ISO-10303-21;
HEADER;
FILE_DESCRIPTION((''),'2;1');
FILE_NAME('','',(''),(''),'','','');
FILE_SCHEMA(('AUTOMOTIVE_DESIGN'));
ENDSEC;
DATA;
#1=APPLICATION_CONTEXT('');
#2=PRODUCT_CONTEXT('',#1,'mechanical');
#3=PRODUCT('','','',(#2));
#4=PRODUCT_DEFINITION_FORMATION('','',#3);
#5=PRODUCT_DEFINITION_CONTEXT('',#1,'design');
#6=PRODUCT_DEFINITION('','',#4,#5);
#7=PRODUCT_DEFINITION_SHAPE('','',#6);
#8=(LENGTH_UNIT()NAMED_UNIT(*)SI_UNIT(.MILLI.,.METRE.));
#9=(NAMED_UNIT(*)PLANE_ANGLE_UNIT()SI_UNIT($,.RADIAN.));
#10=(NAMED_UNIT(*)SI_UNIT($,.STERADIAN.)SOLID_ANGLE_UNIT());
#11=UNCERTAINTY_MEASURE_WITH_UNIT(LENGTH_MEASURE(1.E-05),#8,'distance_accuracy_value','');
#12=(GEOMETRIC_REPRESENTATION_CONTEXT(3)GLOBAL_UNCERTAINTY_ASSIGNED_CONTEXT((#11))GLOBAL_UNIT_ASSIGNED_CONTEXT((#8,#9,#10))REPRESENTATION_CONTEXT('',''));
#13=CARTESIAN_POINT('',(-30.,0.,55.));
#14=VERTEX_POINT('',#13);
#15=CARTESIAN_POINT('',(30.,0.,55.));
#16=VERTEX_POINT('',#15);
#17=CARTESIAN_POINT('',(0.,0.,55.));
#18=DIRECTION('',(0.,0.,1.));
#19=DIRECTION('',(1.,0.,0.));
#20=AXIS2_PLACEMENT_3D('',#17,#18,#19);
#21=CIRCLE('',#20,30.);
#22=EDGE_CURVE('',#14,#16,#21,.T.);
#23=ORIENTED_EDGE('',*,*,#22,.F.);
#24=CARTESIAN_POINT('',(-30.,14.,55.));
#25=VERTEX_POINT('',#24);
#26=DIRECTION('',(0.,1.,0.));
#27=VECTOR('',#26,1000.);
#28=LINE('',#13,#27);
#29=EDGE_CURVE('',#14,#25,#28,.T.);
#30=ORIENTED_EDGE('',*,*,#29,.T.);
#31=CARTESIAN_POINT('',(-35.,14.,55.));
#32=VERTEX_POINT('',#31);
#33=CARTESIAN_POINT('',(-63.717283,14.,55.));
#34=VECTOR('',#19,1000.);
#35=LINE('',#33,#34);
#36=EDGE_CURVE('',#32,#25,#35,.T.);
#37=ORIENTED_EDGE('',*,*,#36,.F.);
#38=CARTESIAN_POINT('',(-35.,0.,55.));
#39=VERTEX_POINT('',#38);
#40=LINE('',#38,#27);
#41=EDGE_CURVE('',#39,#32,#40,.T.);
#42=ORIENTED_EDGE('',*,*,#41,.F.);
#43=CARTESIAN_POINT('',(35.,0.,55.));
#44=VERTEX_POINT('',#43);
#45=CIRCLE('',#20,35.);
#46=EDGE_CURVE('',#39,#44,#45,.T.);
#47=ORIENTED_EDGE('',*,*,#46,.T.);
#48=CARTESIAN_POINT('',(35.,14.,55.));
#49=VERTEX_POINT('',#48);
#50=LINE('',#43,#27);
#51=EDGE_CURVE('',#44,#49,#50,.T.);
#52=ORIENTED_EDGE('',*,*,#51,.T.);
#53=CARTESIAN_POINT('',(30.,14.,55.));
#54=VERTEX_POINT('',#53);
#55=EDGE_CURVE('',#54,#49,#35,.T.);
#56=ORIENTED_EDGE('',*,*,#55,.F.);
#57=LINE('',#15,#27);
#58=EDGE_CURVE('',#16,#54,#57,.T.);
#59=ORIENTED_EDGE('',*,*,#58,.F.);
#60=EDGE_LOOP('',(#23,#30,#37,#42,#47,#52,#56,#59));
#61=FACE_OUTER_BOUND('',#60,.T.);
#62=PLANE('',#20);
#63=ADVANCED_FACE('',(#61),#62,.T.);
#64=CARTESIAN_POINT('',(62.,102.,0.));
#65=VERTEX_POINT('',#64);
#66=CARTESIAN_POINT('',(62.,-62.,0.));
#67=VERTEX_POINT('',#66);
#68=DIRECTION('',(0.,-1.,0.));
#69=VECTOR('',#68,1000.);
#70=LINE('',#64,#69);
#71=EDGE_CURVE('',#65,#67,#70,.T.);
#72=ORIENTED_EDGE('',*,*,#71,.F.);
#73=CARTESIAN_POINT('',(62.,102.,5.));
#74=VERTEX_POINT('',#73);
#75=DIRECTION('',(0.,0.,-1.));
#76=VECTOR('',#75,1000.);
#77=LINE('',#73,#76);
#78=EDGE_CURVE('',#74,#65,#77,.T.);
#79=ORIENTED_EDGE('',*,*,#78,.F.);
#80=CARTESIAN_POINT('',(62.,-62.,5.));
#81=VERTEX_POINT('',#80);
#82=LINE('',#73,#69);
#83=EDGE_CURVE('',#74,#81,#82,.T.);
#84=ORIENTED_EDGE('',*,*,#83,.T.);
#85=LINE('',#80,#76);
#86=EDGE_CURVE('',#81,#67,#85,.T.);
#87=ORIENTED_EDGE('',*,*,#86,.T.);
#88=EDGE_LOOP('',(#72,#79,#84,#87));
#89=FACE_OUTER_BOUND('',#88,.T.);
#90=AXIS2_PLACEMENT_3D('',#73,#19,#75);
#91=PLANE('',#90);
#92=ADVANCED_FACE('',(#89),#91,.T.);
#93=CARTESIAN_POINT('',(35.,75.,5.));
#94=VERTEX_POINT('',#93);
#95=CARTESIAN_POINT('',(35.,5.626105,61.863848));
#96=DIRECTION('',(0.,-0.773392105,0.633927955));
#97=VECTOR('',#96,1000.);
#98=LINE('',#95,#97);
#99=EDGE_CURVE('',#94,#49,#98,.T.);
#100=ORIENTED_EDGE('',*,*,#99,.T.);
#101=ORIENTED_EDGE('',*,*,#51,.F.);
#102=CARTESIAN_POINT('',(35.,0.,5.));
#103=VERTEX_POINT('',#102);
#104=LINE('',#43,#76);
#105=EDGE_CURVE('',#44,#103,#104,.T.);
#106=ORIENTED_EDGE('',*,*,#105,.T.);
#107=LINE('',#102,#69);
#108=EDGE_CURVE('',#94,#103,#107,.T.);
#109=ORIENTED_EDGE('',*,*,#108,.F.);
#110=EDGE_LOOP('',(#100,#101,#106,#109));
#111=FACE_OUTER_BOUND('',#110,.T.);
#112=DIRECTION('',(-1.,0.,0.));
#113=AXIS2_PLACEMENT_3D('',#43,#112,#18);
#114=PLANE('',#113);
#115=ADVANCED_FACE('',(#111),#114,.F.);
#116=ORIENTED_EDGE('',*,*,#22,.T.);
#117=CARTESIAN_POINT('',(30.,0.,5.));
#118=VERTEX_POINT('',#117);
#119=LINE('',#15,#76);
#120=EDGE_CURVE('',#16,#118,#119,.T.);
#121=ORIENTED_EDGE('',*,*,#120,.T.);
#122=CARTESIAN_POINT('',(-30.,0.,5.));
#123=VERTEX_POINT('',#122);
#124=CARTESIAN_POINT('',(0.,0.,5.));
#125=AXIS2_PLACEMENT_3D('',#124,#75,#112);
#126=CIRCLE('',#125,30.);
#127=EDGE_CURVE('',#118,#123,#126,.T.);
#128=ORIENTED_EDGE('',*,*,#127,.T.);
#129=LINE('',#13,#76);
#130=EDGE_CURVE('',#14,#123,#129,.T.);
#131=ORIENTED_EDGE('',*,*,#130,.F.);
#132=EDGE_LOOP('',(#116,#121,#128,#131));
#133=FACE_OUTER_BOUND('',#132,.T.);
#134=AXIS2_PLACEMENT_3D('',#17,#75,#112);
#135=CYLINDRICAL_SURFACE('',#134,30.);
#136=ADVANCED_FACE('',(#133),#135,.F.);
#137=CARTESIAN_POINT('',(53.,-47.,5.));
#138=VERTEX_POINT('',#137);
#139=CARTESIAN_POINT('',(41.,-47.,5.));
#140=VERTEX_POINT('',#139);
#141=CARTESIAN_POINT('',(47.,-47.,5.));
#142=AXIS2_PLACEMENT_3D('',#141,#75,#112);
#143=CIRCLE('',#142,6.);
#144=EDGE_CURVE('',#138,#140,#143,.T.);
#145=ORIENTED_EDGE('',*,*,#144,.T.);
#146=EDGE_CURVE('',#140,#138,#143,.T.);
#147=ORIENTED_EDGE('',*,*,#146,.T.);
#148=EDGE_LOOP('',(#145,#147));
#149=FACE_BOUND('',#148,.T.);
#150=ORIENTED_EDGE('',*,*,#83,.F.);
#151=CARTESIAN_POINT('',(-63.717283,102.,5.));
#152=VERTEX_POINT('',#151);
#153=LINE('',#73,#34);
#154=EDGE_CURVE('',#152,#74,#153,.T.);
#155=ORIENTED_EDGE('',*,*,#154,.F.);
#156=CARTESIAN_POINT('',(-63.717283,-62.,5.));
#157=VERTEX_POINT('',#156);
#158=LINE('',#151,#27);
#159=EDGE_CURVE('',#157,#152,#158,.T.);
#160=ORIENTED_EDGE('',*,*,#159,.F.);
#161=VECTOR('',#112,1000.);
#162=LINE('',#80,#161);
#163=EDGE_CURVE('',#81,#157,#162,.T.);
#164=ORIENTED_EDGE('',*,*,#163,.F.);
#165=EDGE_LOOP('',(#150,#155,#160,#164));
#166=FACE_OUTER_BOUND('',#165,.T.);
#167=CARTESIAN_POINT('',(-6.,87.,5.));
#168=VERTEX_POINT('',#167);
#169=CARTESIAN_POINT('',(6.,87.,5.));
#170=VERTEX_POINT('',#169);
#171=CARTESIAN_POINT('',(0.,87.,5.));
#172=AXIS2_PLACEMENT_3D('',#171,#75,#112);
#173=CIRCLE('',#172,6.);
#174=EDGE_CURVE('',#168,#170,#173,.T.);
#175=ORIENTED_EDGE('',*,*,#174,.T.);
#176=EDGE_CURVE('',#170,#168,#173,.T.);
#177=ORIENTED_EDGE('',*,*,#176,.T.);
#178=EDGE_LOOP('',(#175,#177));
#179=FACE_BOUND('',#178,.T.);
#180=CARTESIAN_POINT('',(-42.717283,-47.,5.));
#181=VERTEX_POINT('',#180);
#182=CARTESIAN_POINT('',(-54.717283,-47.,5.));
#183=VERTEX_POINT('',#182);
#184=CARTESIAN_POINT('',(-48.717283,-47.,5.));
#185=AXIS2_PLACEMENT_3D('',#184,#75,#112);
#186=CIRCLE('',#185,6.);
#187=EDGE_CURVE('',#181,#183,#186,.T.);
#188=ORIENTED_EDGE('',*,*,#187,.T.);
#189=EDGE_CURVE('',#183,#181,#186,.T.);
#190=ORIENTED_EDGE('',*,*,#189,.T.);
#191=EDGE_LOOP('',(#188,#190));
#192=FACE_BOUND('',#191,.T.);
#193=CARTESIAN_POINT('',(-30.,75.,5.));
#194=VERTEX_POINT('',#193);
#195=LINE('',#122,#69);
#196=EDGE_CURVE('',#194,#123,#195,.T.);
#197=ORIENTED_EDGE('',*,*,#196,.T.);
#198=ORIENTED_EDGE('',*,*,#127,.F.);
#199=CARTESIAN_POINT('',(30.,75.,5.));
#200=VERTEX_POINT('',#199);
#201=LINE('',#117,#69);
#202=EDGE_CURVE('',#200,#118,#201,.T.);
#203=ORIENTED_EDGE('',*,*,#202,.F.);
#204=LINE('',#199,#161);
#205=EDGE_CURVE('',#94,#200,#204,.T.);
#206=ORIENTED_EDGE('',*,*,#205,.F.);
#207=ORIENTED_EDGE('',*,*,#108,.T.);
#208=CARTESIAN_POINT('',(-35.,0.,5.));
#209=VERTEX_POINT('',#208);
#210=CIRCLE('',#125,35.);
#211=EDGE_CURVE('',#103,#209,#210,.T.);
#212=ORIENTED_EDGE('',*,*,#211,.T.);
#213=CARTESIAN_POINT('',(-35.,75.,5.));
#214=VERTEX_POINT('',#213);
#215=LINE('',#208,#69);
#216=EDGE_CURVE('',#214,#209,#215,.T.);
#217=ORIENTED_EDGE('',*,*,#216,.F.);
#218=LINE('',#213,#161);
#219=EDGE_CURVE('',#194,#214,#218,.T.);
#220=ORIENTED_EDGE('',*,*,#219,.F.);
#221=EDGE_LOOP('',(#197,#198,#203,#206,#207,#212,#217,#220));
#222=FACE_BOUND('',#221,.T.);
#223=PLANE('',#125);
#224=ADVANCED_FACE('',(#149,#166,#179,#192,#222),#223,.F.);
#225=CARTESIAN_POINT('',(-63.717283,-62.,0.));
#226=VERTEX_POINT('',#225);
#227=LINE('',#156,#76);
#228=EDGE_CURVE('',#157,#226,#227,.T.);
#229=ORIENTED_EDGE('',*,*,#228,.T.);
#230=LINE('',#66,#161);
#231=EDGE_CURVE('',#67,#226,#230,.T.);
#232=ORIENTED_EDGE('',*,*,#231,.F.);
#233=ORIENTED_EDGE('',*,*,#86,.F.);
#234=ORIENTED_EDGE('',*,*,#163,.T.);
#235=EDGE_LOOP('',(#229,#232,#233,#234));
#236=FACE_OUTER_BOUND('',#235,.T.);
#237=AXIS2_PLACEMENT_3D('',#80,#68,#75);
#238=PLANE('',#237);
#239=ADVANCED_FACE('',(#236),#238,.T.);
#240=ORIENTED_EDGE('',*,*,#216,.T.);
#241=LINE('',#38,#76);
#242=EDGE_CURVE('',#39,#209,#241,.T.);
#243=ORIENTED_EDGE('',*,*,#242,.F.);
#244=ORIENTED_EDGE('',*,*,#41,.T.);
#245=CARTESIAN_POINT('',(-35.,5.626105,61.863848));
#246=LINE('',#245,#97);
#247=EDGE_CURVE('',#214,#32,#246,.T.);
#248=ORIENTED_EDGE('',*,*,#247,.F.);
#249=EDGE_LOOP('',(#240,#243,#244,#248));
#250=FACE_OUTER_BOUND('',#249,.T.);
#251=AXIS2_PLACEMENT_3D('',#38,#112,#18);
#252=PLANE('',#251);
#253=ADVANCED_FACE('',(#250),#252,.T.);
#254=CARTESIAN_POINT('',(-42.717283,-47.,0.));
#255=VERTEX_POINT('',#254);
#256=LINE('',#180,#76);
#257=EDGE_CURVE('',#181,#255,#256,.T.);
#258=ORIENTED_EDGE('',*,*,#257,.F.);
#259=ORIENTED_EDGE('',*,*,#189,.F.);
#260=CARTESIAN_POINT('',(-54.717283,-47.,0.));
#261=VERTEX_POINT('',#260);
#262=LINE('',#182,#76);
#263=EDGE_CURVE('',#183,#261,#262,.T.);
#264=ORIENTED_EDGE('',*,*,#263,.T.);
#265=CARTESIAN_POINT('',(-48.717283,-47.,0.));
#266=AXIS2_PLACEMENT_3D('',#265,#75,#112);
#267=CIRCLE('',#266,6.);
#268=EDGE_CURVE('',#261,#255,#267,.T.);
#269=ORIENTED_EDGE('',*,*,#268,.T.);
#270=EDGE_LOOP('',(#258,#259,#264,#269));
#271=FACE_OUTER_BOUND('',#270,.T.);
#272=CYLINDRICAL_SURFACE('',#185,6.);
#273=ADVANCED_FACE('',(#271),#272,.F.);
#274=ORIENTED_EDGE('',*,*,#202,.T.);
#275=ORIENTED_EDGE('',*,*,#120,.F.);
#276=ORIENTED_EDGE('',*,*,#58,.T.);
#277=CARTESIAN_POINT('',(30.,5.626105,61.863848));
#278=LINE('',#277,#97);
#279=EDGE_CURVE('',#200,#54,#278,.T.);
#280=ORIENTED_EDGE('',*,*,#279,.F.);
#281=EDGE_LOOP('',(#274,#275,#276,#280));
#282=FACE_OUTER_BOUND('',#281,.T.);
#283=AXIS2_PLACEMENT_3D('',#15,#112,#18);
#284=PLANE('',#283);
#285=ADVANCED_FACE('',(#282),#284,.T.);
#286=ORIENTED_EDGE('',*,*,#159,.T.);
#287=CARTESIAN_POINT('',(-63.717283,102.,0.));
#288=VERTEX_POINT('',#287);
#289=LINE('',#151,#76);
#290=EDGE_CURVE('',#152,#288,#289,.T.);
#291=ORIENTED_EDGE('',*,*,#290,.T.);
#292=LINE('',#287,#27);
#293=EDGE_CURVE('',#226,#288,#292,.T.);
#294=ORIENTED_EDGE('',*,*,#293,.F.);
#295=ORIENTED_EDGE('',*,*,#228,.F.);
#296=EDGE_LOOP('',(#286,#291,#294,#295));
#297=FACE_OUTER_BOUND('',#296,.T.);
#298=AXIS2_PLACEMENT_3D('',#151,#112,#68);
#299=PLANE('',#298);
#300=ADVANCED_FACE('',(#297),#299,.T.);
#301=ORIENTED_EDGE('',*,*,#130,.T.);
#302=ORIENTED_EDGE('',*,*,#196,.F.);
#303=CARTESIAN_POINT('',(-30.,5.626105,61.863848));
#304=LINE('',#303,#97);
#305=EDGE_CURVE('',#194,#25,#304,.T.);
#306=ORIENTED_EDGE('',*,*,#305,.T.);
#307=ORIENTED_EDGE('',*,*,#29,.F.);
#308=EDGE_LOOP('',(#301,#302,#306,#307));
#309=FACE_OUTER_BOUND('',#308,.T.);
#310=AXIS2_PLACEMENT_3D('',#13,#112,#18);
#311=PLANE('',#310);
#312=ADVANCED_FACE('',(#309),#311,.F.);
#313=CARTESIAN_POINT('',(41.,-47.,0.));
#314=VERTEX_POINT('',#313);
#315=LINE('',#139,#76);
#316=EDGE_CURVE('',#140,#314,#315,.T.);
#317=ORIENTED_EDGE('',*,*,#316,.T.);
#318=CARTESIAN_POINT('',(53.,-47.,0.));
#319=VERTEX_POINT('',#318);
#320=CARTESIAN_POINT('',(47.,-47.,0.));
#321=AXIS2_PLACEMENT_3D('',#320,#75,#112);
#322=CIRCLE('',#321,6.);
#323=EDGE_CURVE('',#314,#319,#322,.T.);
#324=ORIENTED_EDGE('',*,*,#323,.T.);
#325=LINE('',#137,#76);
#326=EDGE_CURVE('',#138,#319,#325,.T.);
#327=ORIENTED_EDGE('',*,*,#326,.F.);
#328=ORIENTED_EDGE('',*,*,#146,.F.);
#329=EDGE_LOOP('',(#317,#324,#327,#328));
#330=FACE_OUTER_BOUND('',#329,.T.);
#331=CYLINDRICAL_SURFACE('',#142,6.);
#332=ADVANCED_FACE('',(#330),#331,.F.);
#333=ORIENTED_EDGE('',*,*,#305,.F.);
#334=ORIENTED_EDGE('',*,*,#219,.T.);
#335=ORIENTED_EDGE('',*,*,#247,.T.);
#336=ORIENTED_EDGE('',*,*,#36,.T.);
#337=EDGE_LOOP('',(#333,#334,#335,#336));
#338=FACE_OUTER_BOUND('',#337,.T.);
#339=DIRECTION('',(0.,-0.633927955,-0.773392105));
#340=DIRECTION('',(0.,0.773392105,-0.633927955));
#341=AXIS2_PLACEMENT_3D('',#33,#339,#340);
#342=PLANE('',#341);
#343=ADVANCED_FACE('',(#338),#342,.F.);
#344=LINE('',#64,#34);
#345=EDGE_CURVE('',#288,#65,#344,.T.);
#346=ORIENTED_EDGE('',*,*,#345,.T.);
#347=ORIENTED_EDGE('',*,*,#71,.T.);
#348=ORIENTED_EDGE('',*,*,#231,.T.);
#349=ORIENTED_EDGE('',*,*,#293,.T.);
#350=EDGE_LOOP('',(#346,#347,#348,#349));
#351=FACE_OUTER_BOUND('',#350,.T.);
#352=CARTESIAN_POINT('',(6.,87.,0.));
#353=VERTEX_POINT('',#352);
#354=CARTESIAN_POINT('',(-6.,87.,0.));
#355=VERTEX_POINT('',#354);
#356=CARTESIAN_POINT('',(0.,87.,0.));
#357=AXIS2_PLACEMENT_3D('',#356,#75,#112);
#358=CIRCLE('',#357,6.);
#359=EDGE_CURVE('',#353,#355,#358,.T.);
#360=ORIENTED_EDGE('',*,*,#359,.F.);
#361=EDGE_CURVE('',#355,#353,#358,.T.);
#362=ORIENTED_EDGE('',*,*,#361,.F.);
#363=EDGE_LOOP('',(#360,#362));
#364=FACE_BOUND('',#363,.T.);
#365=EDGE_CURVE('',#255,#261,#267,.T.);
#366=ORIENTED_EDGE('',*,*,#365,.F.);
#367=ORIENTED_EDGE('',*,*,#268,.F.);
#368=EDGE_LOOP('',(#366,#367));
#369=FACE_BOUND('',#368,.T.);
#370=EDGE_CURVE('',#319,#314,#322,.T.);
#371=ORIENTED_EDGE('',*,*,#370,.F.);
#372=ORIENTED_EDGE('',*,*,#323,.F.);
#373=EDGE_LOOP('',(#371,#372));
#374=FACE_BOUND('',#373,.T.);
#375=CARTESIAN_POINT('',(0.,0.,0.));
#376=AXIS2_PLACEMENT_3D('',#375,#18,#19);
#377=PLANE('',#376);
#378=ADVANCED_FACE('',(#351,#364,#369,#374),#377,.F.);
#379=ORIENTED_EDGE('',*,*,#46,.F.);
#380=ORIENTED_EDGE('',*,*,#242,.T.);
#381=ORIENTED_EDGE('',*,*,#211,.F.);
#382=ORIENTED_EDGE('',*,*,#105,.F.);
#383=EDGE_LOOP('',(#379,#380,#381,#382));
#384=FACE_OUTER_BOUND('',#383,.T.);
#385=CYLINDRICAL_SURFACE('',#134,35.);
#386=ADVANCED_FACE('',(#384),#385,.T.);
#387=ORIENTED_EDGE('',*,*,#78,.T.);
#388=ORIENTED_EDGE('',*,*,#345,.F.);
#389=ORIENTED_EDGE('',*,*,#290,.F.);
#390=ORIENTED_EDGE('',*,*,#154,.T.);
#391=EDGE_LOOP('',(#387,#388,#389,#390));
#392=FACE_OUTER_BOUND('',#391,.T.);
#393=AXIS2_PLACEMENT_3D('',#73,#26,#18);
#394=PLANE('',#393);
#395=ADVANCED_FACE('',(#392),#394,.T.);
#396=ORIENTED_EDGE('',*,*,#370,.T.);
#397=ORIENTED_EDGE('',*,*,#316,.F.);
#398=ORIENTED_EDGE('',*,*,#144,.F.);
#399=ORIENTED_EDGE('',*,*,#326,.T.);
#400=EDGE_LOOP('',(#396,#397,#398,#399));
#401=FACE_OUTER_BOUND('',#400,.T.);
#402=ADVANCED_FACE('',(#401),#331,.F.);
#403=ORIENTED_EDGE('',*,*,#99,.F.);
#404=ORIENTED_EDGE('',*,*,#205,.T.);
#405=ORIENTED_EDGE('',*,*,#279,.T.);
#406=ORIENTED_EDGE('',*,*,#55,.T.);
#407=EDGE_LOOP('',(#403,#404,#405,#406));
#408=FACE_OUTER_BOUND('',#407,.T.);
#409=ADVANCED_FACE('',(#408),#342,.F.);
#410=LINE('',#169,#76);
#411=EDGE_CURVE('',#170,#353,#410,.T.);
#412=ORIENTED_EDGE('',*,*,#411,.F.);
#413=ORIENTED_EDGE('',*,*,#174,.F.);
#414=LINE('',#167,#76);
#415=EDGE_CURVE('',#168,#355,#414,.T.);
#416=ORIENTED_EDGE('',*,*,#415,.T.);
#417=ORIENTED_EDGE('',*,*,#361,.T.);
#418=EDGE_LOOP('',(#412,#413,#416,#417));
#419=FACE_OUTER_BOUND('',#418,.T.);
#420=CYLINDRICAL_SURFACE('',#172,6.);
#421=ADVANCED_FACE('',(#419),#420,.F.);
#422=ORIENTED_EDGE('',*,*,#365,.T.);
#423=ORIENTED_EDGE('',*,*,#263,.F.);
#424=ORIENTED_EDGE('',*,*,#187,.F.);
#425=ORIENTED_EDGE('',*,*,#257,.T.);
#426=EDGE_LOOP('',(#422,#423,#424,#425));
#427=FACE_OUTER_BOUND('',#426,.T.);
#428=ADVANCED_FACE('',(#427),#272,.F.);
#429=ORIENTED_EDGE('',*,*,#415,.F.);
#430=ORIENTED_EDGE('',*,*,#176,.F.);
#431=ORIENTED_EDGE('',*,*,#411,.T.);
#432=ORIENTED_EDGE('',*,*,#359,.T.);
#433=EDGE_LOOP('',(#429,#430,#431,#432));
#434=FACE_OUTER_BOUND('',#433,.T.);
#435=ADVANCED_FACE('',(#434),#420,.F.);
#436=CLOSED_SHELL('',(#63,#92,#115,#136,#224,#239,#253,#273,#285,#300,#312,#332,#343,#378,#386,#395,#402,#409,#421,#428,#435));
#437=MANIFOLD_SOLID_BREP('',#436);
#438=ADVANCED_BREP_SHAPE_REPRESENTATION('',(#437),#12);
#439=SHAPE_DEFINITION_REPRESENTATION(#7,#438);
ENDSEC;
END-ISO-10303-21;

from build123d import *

# Parameters (mm, degrees)
U_CHANNEL_DEPTH         = 55
FLANGE_PLATE_SKETCH_W   = 125.717283216
FLANGE_PLATE_SKETCH_H   = 164
FLANGE_PLATE_SKETCH_R   = 6
FLANGE_PLATE_DEPTH      = 5
CHANNEL_SIDE_TRIM_DEPTH = 171.979049299


with BuildPart() as part:
    # U-Channel Profile Sketch → U-Channel (new body)
    with BuildSketch(Plane.XY):
        with BuildLine():
            Line((35, 0), (35, 75))
            Line((35, 75), (30, 75))
            Line((30, 75), (30, 0))
            ThreePointArc((30, 0), (0, -30), (-30, 0))
            Line((-30, 0), (-30, 75))
            Line((-30, 75), (-35, 75))
            Line((-35, 75), (-35, 0))
            ThreePointArc((-35, 0), (0, -35), (35, 0))
        make_face()
    extrude(amount=U_CHANNEL_DEPTH)

    # Flange Plate Sketch → Flange Plate (add)
    with BuildSketch(Plane(origin=(0, 0, 0), x_dir=(-1, 0, 0), z_dir=(0, 0, -1))):
        with Locations((0.858641608, 20)):
            Rectangle(FLANGE_PLATE_SKETCH_W, FLANGE_PLATE_SKETCH_H)
        with Locations((48.717283216, -47)):
            Circle(FLANGE_PLATE_SKETCH_R, mode=Mode.SUBTRACT)
        with Locations((-47, -47)):
            Circle(FLANGE_PLATE_SKETCH_R, mode=Mode.SUBTRACT)
        with Locations((0, 87)):
            Circle(FLANGE_PLATE_SKETCH_R, mode=Mode.SUBTRACT)
    extrude(amount=-FLANGE_PLATE_DEPTH)

    # Channel Side Trim Sketch → Channel Side Trim (cut, through all)
    with BuildSketch(Plane(origin=(62, 0, 0), x_dir=(0, 0, -1), z_dir=(1, 0, 0))):
        Polygon((-55, 14), (-5, 75), (-55, 75), align=None)
    extrude(amount=-CHANNEL_SIDE_TRIM_DEPTH, mode=Mode.SUBTRACT)


solid = part.part
